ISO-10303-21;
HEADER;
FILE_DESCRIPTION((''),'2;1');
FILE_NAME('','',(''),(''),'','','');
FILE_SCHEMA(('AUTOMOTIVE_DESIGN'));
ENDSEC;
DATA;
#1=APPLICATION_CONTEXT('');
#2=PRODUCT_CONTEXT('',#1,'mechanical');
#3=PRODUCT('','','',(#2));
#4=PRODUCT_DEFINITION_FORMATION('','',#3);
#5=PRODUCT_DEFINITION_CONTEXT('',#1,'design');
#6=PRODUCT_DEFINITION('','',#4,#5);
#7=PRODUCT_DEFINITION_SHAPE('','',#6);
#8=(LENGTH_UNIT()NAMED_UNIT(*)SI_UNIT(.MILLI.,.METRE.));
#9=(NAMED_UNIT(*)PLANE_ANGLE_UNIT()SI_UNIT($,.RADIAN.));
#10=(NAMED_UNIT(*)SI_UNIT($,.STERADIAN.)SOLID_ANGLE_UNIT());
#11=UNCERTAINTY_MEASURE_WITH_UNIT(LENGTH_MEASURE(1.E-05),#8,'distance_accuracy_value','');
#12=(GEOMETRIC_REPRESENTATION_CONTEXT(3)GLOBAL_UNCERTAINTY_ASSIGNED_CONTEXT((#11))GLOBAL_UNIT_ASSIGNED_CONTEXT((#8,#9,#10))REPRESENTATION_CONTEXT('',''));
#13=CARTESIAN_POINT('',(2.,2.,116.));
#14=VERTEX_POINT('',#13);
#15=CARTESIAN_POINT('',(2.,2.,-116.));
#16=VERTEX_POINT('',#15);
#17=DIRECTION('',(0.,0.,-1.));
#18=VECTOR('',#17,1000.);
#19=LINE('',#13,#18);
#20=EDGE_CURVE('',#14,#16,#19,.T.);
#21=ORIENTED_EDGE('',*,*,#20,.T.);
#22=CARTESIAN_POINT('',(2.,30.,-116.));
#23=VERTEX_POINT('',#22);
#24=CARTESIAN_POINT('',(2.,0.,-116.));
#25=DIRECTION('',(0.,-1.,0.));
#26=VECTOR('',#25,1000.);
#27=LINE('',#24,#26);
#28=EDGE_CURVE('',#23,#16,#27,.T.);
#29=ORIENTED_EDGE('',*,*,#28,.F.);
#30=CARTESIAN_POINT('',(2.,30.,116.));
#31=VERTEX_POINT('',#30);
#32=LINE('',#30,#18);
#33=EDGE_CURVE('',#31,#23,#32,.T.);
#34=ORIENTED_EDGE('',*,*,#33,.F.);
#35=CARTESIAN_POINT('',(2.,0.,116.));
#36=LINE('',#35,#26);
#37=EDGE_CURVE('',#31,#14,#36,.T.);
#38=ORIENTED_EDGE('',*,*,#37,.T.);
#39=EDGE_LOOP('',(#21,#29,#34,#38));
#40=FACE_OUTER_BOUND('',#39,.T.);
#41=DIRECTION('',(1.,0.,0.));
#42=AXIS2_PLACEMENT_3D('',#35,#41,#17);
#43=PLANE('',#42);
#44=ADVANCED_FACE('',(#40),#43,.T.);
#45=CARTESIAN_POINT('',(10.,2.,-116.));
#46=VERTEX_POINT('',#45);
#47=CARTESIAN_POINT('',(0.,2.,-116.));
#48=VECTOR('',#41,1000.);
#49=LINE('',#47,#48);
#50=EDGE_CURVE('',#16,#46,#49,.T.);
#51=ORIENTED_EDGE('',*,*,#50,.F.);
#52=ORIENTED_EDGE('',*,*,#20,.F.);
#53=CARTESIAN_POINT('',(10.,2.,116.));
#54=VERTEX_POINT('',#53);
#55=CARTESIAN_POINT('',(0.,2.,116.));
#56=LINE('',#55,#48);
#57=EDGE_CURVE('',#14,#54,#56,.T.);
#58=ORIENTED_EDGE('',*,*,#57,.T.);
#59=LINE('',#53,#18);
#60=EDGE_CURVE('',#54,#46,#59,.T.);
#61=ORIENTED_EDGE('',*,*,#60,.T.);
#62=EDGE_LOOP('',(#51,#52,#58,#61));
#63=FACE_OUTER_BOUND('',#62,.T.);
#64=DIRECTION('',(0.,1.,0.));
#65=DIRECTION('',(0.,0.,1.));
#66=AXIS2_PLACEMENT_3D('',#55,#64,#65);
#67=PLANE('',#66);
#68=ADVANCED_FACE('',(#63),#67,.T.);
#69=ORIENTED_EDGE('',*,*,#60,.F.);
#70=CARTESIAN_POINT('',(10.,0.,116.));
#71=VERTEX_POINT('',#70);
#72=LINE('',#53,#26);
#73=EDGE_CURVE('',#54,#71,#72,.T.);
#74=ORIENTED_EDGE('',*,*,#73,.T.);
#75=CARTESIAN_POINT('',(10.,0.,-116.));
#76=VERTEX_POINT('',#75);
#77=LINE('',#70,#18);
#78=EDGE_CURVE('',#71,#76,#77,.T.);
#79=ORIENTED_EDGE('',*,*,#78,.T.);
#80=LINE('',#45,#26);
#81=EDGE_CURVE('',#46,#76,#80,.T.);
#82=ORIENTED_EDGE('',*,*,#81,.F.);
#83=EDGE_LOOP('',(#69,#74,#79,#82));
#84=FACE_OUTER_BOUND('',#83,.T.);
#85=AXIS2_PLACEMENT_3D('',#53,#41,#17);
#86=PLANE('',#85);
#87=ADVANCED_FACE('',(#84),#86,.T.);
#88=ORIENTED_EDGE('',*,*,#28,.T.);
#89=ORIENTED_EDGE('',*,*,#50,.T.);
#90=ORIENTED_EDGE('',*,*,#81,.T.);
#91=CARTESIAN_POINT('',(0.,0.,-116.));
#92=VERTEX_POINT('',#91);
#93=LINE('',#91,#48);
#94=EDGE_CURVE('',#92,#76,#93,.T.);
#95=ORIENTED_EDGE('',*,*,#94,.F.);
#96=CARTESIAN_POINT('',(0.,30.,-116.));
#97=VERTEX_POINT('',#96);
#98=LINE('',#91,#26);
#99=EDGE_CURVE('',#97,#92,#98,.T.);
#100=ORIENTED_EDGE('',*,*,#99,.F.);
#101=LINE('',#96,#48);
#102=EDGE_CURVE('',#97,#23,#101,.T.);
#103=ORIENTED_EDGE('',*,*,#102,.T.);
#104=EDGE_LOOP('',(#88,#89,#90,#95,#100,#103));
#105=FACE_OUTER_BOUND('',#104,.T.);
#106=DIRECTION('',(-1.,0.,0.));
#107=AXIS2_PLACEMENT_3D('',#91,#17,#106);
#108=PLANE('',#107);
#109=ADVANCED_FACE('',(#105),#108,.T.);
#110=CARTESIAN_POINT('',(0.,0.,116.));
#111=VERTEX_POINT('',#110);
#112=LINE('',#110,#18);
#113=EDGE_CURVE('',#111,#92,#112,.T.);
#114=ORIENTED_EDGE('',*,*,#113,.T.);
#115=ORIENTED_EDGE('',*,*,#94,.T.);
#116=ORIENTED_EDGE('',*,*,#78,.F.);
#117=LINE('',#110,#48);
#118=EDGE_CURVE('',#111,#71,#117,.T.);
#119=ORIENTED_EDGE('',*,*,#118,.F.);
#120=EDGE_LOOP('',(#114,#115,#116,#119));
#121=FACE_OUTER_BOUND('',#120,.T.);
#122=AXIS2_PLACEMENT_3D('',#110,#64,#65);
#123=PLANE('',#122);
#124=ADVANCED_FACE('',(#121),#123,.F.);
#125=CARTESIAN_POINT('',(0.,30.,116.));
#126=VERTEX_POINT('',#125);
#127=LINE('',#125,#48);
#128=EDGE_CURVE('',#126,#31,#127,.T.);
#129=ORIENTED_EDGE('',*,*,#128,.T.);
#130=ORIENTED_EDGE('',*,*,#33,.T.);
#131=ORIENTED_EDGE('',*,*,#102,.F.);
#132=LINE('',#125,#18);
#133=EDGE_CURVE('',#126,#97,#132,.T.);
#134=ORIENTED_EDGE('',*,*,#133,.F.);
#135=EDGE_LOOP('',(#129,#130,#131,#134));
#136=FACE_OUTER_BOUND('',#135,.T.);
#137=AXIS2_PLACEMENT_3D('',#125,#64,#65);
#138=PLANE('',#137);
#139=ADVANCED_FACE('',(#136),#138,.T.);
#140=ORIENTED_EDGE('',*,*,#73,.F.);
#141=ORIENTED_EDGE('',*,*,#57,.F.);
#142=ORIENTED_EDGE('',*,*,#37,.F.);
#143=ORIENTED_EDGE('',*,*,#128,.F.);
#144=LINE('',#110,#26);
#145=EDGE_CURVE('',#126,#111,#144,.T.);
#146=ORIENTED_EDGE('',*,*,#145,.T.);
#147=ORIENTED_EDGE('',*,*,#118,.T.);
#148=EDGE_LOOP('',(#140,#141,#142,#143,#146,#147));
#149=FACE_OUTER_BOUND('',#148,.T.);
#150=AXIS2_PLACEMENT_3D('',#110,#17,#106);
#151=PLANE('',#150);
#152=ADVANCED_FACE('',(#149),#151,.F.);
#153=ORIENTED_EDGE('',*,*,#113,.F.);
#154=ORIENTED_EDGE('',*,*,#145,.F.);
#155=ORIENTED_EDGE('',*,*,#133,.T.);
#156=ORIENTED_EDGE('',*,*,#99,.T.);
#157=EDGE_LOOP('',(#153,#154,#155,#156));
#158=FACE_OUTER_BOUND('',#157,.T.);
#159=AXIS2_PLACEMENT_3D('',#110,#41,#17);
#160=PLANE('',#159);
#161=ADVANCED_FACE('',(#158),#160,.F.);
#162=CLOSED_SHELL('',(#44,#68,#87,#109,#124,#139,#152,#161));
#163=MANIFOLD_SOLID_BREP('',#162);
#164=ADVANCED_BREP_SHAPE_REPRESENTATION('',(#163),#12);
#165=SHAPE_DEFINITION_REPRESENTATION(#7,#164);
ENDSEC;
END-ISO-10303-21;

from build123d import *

# Parameters (mm, degrees)
EXTRUDE_1_DEPTH = 116


with BuildPart() as part:
    # 草图1 → 拉伸-薄壁1 (new, symmetric)
    with BuildSketch(Plane.XY):
        Polygon((10, 0), (0, 0), (0, 30), (2, 30), (2, 2), (10, 2), align=None)
    extrude(amount=EXTRUDE_1_DEPTH, both=True)


solid = part.part
